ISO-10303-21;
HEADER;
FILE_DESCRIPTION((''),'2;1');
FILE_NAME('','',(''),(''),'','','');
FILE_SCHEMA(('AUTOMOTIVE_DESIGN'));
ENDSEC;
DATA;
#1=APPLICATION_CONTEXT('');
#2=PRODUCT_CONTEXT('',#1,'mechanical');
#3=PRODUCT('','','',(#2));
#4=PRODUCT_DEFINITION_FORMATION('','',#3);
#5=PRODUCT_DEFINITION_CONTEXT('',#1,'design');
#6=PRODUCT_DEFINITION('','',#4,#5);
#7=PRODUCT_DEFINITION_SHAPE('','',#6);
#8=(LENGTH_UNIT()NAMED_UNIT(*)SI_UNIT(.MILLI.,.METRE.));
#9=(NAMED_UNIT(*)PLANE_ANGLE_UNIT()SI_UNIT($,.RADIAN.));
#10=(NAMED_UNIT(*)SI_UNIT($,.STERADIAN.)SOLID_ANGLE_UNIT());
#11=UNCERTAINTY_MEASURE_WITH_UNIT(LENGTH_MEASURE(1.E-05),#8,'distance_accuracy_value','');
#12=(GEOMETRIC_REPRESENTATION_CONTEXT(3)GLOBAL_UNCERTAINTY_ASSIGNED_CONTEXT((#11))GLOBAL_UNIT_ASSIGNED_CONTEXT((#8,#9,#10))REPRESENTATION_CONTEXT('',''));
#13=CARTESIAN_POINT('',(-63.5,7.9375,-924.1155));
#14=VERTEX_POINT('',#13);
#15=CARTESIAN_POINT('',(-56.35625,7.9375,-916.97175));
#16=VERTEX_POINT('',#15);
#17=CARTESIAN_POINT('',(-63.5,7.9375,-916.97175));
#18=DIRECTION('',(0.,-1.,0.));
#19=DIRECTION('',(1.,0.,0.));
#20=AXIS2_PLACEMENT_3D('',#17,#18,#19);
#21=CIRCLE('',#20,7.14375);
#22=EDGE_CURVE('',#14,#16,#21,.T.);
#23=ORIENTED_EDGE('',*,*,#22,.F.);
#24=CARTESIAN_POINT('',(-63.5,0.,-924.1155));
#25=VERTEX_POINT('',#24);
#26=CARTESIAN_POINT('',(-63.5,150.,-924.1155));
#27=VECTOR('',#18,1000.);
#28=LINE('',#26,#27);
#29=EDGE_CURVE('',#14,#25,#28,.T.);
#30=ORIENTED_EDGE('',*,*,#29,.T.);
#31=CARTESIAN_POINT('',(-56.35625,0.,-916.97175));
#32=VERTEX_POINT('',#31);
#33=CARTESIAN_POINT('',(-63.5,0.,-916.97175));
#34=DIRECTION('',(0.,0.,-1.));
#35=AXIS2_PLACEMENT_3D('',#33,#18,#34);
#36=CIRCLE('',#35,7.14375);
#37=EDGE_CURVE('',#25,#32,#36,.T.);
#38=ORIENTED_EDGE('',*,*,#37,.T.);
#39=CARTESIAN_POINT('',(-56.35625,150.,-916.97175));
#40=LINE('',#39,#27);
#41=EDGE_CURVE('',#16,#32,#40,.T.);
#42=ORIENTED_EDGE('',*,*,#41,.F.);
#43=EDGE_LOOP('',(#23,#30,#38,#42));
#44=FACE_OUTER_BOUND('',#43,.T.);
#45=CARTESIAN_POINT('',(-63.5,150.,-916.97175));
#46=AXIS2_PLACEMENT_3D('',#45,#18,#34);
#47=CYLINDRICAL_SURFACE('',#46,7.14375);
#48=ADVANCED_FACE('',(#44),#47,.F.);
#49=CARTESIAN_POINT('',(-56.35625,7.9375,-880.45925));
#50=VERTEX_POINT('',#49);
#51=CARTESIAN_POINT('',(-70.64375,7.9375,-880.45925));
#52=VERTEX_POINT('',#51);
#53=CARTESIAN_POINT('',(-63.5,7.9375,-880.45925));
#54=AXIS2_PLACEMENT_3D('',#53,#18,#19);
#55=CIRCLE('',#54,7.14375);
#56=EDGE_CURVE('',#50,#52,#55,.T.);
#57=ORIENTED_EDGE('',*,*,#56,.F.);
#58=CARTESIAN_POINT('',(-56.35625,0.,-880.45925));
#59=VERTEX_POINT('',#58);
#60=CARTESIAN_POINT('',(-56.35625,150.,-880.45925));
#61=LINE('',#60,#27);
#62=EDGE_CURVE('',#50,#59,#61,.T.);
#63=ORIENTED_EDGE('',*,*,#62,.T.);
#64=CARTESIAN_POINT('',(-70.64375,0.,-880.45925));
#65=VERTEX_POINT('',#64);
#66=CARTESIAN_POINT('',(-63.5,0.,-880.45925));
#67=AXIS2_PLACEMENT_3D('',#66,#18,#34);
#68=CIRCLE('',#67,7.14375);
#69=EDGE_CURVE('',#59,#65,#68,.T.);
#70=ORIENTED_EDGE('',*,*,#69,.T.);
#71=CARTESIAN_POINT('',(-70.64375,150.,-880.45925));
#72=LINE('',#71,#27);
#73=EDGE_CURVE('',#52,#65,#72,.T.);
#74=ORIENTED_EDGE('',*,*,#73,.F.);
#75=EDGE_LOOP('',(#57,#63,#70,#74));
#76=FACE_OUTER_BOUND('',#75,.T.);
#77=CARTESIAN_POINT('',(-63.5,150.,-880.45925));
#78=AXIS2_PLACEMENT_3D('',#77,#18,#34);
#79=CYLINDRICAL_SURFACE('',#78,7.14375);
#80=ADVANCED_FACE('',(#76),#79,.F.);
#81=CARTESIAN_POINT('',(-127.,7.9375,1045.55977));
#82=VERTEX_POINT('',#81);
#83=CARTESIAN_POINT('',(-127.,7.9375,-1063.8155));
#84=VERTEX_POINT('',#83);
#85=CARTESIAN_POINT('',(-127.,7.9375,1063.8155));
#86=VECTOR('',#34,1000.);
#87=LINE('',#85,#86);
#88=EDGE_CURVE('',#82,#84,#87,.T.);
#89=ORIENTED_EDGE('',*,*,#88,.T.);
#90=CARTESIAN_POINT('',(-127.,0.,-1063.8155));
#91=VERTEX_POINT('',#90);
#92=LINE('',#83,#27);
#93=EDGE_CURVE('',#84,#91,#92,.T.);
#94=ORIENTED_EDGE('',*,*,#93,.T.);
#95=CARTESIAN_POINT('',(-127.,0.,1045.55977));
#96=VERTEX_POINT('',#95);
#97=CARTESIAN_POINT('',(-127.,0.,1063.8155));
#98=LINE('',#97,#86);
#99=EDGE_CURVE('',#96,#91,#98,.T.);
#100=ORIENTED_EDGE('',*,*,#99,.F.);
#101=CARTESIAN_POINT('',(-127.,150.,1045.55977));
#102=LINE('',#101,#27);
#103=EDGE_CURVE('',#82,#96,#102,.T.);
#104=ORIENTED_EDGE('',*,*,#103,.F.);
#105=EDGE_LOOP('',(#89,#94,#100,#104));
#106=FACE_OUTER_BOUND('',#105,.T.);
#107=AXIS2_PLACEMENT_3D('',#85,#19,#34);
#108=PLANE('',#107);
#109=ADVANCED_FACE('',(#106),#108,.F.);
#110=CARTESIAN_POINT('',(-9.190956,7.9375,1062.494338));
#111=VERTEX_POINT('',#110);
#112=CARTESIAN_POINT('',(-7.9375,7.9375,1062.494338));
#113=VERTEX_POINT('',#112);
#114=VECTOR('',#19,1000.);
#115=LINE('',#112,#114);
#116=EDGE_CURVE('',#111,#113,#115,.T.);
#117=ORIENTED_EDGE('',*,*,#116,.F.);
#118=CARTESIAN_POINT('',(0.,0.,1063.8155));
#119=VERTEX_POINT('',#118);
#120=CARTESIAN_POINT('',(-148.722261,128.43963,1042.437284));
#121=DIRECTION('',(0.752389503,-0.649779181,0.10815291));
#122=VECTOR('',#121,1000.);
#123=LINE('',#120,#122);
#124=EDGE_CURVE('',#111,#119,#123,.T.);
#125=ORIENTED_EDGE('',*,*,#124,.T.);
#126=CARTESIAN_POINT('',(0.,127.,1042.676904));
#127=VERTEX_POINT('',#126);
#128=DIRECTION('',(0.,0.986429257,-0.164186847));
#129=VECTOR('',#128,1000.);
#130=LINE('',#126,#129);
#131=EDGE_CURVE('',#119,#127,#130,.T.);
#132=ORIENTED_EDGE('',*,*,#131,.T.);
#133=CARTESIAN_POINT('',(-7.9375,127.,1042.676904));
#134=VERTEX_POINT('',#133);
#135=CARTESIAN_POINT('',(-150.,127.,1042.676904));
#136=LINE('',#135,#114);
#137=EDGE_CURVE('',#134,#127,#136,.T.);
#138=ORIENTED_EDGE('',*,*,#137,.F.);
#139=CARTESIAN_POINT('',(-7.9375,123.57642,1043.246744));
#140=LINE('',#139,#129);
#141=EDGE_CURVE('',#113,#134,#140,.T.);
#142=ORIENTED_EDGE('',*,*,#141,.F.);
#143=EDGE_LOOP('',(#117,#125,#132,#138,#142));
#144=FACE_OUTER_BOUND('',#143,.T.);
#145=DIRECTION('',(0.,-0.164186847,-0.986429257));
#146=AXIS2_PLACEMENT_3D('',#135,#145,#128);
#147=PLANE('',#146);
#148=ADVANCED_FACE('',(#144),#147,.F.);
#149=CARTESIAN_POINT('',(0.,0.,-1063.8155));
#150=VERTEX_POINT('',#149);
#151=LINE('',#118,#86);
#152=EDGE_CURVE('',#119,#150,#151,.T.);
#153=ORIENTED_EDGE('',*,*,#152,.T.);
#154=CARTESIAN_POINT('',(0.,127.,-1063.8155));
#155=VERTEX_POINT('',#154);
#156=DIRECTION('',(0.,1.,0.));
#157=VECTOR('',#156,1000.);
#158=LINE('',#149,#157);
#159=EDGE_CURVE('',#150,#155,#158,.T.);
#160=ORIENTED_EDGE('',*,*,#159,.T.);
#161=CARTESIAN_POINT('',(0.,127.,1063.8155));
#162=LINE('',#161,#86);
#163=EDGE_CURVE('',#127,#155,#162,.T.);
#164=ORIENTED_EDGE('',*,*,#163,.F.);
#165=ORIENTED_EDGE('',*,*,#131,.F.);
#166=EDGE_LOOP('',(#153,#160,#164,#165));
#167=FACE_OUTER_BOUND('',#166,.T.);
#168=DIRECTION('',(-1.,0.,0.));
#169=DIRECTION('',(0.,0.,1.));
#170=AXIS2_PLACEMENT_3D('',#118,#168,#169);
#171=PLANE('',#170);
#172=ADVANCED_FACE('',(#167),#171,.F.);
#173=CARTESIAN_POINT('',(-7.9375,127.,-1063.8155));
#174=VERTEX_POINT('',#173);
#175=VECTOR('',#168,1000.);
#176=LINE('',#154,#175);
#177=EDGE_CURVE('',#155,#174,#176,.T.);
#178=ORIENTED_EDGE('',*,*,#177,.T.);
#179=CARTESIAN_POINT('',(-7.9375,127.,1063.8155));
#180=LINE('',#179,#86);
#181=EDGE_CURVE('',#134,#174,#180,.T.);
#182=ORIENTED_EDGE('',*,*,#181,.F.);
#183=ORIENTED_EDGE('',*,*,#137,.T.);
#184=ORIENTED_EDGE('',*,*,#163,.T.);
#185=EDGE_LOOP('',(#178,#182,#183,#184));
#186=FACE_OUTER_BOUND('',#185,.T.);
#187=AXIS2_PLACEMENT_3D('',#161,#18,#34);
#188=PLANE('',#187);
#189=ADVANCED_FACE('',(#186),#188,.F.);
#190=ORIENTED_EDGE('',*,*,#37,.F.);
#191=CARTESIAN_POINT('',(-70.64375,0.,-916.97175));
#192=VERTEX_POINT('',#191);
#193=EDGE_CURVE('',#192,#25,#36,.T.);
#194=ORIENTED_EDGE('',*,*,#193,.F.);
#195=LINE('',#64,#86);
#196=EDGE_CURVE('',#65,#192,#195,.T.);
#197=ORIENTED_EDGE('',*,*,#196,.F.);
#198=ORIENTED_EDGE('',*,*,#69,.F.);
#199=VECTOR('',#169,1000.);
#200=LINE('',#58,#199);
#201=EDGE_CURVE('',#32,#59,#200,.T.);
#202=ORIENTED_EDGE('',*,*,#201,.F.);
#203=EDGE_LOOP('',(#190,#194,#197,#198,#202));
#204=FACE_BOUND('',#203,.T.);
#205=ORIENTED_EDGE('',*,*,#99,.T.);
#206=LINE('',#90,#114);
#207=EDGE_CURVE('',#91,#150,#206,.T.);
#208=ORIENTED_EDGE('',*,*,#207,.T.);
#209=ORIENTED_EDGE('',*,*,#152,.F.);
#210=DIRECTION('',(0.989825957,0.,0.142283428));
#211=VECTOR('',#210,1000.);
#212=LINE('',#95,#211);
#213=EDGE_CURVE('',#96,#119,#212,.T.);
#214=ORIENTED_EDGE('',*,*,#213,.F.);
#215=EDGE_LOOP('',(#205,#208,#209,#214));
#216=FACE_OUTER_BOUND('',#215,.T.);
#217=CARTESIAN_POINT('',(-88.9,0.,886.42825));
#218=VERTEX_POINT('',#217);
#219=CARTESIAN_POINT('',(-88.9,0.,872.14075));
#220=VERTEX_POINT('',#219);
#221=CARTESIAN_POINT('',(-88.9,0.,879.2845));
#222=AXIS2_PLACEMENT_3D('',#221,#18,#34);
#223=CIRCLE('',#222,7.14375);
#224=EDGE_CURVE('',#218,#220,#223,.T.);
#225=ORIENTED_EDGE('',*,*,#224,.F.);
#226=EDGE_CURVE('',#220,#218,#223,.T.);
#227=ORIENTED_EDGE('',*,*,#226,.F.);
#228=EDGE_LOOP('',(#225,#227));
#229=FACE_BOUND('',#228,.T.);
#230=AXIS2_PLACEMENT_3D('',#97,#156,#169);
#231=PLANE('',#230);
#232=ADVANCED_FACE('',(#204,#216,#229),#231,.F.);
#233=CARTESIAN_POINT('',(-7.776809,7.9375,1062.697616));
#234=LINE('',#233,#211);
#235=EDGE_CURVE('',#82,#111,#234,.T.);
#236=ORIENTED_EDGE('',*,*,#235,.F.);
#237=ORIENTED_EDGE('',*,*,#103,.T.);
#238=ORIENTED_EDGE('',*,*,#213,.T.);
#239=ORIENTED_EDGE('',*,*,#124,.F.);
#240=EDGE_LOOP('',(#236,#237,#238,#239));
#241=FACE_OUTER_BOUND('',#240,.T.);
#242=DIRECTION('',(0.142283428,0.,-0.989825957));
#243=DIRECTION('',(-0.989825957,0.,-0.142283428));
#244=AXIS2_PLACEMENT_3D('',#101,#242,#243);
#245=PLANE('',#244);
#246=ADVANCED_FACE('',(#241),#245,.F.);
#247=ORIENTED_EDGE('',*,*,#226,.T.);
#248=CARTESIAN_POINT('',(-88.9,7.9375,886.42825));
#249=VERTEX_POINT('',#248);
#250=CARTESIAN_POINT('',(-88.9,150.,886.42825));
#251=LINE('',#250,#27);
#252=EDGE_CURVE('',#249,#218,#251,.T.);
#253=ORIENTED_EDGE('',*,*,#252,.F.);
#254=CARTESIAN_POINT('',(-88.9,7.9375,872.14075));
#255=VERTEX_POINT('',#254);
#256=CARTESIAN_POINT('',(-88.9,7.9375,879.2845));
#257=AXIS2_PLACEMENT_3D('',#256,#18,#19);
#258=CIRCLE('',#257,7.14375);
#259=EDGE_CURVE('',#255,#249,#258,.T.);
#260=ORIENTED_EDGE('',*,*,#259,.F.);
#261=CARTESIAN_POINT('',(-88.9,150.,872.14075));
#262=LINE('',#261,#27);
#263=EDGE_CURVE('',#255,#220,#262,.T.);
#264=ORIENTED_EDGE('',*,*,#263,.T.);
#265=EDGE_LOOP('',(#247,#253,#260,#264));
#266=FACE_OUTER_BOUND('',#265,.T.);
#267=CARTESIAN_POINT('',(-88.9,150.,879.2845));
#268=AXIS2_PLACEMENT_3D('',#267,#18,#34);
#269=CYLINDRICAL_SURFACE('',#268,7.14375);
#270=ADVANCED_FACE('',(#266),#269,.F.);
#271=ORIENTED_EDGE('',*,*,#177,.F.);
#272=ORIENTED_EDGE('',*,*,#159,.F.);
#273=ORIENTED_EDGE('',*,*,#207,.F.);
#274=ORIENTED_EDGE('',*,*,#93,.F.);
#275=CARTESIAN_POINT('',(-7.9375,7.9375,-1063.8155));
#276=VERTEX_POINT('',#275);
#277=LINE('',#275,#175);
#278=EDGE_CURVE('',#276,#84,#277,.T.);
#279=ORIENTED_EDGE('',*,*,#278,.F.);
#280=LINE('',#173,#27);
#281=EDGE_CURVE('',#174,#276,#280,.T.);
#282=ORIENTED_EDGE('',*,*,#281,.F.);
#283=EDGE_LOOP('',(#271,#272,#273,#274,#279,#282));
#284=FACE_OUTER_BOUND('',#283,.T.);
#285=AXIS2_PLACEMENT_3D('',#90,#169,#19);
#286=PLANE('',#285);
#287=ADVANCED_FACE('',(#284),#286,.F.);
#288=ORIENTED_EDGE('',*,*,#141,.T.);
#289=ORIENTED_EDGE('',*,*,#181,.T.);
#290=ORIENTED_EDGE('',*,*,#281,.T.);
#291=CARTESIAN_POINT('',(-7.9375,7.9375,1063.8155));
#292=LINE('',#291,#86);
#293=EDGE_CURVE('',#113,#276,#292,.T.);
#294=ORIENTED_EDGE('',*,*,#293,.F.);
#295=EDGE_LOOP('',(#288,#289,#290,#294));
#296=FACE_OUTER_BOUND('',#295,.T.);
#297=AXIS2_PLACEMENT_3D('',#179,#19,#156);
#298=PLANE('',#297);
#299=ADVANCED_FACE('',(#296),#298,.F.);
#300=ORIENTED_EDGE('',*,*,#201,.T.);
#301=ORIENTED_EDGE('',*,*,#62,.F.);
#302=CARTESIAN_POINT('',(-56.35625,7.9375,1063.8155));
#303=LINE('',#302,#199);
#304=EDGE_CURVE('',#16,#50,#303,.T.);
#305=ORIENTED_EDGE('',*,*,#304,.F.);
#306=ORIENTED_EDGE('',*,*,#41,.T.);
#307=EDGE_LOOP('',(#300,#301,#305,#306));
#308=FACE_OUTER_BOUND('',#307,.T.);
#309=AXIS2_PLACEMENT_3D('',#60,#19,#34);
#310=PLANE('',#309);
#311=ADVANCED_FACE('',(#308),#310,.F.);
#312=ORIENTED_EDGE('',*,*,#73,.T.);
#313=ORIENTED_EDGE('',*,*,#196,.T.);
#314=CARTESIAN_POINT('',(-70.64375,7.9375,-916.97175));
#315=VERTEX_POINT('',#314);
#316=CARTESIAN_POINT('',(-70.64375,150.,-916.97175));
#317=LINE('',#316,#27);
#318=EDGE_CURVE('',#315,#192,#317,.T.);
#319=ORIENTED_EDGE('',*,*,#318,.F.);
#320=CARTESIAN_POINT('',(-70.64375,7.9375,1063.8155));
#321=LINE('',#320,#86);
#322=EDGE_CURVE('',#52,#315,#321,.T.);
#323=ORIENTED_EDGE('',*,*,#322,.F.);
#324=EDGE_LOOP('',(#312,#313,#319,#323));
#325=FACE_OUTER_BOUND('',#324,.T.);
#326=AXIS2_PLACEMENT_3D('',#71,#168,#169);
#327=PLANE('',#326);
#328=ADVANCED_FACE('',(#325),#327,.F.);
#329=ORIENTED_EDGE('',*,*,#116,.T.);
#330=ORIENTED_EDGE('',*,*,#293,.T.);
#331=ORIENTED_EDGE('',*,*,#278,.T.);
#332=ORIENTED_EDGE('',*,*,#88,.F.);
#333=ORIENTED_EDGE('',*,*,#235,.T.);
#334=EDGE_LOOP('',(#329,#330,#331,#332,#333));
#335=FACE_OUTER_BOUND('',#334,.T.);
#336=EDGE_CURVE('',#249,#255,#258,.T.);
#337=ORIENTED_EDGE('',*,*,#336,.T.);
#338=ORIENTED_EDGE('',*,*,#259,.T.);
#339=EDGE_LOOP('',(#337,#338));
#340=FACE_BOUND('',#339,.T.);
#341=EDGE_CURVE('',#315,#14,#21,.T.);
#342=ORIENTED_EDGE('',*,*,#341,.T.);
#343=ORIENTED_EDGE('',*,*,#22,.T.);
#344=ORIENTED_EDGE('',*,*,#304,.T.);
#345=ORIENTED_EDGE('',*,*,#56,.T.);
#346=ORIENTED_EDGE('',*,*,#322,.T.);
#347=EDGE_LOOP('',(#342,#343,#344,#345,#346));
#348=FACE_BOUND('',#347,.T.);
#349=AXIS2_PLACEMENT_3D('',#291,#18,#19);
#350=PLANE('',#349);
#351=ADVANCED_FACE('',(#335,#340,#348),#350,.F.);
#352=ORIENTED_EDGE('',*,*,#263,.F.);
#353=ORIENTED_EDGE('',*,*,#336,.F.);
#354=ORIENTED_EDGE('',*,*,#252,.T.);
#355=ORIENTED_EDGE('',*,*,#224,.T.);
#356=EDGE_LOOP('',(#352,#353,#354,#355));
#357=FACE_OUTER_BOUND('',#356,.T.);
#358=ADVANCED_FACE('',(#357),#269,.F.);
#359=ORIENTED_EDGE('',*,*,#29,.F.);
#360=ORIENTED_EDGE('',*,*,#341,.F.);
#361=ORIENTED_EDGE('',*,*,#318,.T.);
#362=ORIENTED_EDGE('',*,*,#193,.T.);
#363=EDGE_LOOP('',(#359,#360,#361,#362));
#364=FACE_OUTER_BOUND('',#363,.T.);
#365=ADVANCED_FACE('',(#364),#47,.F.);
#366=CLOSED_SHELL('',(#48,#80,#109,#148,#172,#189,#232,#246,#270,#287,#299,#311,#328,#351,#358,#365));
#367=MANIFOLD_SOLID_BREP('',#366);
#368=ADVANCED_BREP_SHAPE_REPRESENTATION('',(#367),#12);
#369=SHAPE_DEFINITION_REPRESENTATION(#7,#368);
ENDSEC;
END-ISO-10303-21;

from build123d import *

# Parameters (mm, degrees)
BOSS_EXTRUDE1_DEPTH = 1063.8155
CUT_EXTRUDE1_DEPTH  = 150
SKETCH3_R           = 7.14375
CUT_EXTRUDE2_DEPTH  = 150


with BuildPart() as part:
    # Sketch1 → Boss-Extrude1 (new, symmetric)
    with BuildSketch(Plane.XY):
        Polygon((-127, 0), (0, 0), (0, 127), (-7.9375, 127), (-7.9375, 7.9375), (-127, 7.9375), align=None)
    extrude(amount=BOSS_EXTRUDE1_DEPTH, both=True)

    # Sketch2 → Cut-Extrude1 (cut)
    with BuildSketch(Plane(origin=(0, 0, 0), x_dir=(0, 0, -1), z_dir=(1, 0, 0))):
        Polygon((-1063.8155, 0), (-1063.8155, 127), (-1042.676904036, 127), align=None)
    extrude(amount=-CUT_EXTRUDE1_DEPTH, mode=Mode.SUBTRACT)

    # Sketch3 → Cut-Extrude2 (cut)
    with BuildSketch(Plane.XZ):
        with Locations(Location((-88.9, 879.2845, 0), (0, 0, 270))):
            Circle(SKETCH3_R)
        Polygon((0, 1063.8155), (-127, 1063.8155), (-127, 1045.559770079), align=None)
        with BuildLine():
            Line((-56.35625, -880.45925), (-56.35625, -916.97175))
            ThreePointArc((-56.35625, -916.97175), (-63.5, -924.1155), (-70.64375, -916.97175))
            Line((-70.64375, -916.97175), (-70.64375, -880.45925))
            ThreePointArc((-70.64375, -880.45925), (-63.5, -873.3155), (-56.35625, -880.45925))
        make_face()
    extrude(amount=-CUT_EXTRUDE2_DEPTH, mode=Mode.SUBTRACT)


solid = part.part
